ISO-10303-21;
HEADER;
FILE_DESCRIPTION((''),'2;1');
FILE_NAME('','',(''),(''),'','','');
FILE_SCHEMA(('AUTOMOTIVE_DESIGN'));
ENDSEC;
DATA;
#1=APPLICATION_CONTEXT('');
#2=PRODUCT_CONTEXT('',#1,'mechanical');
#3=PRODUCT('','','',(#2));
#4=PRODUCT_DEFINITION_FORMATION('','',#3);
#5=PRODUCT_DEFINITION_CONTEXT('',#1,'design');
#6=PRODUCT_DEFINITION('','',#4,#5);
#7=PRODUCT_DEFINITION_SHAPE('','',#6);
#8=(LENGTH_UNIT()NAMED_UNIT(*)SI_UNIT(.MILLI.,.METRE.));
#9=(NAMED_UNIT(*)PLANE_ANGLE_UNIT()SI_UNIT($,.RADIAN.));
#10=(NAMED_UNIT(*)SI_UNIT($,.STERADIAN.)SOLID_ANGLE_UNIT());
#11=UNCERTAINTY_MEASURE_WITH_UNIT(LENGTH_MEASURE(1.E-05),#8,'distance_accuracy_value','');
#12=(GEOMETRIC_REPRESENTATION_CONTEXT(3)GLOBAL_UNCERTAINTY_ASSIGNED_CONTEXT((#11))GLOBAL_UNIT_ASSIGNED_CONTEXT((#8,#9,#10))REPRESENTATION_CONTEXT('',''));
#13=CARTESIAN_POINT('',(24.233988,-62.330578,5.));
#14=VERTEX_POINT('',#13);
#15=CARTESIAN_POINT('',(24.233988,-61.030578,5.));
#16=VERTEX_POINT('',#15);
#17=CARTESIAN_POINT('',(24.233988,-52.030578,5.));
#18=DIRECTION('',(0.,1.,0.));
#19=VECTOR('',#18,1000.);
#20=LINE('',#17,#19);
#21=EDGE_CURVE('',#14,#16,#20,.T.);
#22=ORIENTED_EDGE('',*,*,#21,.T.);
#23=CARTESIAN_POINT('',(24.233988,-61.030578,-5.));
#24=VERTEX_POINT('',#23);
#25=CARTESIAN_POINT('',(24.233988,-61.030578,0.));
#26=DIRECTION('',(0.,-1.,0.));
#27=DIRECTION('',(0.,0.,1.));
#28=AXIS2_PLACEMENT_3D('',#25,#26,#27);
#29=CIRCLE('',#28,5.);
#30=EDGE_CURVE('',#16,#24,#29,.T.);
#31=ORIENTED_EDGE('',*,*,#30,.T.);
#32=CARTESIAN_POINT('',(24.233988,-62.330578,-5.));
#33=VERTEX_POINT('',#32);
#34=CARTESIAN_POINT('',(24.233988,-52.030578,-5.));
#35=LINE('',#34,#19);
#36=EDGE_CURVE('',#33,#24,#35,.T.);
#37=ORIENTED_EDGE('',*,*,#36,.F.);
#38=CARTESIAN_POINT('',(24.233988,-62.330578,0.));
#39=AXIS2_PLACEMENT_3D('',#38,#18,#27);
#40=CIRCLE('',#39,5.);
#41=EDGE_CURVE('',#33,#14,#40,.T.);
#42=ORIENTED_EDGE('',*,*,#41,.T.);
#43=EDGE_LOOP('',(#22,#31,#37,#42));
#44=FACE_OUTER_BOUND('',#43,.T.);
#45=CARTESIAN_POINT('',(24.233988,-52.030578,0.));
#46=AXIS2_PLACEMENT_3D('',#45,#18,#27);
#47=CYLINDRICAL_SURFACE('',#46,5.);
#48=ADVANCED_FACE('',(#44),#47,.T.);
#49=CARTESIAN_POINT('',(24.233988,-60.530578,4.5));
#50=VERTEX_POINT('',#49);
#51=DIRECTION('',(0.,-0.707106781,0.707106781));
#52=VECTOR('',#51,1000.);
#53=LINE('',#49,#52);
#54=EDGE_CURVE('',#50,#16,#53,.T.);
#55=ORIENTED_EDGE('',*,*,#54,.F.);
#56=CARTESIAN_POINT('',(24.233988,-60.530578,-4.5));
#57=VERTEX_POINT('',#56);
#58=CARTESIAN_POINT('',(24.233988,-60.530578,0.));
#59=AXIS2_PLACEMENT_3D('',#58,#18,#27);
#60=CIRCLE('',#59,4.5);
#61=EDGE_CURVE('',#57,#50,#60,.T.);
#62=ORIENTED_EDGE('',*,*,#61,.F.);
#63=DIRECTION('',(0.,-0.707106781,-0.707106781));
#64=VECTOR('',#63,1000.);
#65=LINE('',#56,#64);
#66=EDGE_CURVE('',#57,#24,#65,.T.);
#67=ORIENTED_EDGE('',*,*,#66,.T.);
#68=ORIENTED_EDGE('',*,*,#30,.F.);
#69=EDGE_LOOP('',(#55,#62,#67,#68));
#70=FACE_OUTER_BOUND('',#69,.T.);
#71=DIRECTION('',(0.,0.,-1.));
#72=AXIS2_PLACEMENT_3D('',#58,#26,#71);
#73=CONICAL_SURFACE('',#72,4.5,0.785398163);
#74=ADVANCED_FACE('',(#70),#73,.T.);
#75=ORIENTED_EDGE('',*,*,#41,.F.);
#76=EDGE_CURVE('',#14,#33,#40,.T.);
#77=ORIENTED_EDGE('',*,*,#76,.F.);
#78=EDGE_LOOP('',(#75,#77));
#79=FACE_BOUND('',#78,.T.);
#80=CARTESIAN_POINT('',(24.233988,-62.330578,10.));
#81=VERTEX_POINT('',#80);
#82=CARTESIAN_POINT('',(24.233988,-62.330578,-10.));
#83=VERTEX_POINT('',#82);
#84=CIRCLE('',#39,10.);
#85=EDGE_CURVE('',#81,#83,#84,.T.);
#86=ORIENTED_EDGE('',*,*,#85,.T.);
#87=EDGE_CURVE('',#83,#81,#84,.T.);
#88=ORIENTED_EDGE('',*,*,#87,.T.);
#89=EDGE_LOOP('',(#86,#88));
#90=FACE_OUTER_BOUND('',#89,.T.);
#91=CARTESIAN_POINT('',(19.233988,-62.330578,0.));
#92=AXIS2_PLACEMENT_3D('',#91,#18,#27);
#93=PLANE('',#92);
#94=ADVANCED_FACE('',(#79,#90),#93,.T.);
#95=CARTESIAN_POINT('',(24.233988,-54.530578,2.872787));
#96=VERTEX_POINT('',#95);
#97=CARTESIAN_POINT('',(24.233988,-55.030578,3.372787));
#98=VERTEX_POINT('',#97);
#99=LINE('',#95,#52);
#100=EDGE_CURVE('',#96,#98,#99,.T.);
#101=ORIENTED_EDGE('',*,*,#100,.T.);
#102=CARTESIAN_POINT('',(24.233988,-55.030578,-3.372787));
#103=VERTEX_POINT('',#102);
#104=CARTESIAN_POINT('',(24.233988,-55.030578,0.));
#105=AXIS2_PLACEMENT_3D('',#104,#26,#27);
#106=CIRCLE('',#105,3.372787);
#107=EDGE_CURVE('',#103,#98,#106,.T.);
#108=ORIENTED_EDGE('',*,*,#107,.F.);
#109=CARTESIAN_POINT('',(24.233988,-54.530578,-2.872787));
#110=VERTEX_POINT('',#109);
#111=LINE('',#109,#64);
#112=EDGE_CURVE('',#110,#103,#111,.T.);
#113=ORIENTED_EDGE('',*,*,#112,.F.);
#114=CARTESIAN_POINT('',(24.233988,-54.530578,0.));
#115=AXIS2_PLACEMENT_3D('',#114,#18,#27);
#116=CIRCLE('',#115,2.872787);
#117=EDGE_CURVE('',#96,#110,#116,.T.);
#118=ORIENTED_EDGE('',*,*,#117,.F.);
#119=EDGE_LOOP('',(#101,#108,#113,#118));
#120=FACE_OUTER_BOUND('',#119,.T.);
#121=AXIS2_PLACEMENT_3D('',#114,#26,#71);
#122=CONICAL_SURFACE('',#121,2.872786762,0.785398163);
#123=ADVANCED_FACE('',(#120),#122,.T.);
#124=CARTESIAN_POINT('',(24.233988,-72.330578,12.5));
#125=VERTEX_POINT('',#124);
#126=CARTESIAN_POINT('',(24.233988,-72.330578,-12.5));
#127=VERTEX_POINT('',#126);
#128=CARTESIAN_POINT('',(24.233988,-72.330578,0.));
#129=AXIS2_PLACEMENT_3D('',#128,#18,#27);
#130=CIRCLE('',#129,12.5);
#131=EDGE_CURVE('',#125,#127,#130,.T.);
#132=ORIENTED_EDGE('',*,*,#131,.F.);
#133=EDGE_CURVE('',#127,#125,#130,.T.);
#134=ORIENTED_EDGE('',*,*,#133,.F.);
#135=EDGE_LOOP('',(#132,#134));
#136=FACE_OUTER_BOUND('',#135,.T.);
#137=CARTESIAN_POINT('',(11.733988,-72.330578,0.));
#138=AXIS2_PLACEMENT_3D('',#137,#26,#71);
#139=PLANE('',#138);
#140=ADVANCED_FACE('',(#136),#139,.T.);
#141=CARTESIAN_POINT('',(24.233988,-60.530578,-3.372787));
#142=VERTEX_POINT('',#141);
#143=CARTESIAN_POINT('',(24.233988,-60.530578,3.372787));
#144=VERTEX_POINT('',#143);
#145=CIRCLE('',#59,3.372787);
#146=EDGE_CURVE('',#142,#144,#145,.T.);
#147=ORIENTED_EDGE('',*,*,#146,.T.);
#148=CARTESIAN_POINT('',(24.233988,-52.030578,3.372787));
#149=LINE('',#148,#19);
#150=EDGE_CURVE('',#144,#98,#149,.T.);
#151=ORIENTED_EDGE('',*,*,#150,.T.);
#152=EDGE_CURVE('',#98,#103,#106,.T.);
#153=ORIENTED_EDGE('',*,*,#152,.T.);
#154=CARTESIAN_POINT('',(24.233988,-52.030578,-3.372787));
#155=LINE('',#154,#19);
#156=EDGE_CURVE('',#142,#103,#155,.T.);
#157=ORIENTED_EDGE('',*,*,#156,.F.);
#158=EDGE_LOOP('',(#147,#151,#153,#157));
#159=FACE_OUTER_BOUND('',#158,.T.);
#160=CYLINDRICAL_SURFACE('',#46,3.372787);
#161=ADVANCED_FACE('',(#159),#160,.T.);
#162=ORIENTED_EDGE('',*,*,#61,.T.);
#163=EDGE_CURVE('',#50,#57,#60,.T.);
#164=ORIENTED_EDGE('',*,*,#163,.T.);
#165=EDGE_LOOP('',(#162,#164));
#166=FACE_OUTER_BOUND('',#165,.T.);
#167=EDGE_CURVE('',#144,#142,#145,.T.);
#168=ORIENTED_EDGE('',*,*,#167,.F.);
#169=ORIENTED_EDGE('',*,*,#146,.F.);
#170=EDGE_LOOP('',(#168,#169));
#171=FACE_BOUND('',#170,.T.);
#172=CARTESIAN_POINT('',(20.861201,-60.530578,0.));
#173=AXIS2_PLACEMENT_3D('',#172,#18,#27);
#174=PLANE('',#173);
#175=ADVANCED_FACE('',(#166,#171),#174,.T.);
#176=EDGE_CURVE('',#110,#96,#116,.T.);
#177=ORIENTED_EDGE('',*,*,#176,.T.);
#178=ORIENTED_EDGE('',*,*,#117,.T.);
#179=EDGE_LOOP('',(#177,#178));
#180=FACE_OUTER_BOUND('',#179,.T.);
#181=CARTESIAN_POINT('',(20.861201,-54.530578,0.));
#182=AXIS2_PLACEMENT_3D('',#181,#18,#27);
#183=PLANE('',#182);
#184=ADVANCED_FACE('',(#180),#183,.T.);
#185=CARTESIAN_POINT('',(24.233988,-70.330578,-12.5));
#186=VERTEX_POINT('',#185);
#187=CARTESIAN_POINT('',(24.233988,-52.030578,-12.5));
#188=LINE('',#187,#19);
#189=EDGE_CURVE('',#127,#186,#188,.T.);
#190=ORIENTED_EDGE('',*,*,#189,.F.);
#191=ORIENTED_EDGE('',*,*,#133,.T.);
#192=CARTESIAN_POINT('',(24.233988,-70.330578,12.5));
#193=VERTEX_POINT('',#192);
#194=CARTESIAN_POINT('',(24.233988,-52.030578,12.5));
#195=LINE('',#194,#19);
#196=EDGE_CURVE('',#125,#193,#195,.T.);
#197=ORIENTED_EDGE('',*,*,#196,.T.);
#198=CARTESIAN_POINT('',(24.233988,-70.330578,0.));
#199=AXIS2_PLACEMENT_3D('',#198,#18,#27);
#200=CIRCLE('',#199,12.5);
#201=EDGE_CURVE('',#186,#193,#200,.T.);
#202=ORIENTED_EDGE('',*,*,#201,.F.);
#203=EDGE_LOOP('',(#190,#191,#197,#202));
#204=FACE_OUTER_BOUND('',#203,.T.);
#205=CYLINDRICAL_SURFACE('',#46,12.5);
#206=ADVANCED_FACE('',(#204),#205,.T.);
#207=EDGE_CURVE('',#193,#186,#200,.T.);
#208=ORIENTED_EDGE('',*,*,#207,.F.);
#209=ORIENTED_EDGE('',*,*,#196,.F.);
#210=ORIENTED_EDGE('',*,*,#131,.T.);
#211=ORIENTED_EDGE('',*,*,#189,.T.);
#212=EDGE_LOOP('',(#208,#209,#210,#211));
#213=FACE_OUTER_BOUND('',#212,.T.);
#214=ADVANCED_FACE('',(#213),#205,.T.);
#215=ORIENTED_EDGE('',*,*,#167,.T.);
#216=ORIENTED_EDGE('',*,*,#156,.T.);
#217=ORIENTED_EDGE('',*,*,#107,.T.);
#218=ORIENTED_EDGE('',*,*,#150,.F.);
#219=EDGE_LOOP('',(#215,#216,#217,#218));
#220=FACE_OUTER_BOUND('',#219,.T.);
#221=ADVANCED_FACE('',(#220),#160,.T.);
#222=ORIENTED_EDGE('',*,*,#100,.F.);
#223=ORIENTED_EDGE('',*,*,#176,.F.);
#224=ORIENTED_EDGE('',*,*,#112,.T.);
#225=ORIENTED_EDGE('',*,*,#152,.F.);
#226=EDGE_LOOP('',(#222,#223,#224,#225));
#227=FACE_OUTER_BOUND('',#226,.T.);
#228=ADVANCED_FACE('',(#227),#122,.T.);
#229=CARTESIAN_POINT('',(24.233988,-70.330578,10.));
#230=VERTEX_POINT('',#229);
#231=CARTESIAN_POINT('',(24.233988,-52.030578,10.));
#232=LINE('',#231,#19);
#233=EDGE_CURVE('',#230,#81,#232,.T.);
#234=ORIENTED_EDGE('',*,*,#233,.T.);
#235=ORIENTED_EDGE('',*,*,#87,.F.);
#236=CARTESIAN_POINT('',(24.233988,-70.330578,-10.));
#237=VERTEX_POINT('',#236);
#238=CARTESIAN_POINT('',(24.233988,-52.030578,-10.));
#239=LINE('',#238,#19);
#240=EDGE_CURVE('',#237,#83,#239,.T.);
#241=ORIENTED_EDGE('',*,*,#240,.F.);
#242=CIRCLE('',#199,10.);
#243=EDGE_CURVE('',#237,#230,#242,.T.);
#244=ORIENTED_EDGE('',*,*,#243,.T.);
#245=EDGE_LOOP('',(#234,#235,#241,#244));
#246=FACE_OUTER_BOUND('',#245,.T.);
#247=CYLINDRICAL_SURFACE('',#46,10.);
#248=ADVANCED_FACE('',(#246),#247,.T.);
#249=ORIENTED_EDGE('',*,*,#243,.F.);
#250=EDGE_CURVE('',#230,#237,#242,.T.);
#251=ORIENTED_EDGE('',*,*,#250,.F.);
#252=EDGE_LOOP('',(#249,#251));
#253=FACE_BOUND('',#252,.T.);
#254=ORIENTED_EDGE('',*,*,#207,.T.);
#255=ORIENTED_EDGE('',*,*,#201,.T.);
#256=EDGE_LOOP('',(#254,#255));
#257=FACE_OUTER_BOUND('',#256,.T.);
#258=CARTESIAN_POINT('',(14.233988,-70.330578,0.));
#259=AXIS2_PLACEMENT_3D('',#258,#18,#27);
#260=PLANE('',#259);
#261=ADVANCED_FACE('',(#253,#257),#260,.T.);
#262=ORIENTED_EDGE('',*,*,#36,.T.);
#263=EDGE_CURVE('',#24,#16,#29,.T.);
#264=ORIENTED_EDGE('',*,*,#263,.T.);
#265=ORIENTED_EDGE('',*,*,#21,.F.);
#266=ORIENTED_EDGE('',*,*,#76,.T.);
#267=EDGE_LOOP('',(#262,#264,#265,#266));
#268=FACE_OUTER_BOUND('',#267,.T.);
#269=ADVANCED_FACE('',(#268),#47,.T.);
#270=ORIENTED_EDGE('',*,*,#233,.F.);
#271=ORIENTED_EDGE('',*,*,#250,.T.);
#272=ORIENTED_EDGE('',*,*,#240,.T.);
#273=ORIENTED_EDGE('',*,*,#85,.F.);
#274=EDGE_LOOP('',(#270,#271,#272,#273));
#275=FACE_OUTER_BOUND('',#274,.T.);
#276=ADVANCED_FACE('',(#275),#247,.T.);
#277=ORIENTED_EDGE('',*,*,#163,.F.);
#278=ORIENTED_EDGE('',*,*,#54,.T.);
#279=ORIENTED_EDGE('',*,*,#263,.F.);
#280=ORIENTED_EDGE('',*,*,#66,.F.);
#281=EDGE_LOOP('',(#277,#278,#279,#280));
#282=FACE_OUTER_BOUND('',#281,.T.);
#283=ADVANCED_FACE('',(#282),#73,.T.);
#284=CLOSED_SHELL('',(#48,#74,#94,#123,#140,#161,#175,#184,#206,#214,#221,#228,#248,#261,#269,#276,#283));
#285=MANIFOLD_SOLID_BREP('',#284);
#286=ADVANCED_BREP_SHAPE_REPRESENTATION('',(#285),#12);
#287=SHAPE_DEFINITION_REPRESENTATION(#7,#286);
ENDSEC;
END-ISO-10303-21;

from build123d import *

# Parameters (mm, degrees)
CHAMFER1_SIZE = 0.5


with BuildPart() as part:
    # Sketch1 → Revolve8 (revolve)
    with BuildSketch(Plane.XY, mode=Mode.PRIVATE) as revolve8_sk:
        Polygon((20.861200947, -54.530577635), (24.233987709, -54.530577635), (24.233987709, -72.330577635), (11.733987709, -72.330577635), (11.733987709, -70.330577635), (14.233987709, -70.330577635), (14.233987709, -62.330577635), (19.233987709, -62.330577635), (19.233987709, -60.530577635), (20.861200947, -60.530577635), align=None)
    revolve(revolve8_sk.sketch.rotate(Axis((24.233987709, -52.030577635, 0), (0, -1, 0)), 270), axis=Axis((24.233987709, -52.030577635, 0), (0, -1, 0)))

    # Chamfer1
    chamfer1_edges = [part.edges().sort_by_distance(p)[0] for p in [
        (24.233987709, -54.530577635, -3.372786762),
        (24.233987709, -60.530577635, -5),
    ]]
    chamfer(chamfer1_edges, length=CHAMFER1_SIZE)


solid = part.part
